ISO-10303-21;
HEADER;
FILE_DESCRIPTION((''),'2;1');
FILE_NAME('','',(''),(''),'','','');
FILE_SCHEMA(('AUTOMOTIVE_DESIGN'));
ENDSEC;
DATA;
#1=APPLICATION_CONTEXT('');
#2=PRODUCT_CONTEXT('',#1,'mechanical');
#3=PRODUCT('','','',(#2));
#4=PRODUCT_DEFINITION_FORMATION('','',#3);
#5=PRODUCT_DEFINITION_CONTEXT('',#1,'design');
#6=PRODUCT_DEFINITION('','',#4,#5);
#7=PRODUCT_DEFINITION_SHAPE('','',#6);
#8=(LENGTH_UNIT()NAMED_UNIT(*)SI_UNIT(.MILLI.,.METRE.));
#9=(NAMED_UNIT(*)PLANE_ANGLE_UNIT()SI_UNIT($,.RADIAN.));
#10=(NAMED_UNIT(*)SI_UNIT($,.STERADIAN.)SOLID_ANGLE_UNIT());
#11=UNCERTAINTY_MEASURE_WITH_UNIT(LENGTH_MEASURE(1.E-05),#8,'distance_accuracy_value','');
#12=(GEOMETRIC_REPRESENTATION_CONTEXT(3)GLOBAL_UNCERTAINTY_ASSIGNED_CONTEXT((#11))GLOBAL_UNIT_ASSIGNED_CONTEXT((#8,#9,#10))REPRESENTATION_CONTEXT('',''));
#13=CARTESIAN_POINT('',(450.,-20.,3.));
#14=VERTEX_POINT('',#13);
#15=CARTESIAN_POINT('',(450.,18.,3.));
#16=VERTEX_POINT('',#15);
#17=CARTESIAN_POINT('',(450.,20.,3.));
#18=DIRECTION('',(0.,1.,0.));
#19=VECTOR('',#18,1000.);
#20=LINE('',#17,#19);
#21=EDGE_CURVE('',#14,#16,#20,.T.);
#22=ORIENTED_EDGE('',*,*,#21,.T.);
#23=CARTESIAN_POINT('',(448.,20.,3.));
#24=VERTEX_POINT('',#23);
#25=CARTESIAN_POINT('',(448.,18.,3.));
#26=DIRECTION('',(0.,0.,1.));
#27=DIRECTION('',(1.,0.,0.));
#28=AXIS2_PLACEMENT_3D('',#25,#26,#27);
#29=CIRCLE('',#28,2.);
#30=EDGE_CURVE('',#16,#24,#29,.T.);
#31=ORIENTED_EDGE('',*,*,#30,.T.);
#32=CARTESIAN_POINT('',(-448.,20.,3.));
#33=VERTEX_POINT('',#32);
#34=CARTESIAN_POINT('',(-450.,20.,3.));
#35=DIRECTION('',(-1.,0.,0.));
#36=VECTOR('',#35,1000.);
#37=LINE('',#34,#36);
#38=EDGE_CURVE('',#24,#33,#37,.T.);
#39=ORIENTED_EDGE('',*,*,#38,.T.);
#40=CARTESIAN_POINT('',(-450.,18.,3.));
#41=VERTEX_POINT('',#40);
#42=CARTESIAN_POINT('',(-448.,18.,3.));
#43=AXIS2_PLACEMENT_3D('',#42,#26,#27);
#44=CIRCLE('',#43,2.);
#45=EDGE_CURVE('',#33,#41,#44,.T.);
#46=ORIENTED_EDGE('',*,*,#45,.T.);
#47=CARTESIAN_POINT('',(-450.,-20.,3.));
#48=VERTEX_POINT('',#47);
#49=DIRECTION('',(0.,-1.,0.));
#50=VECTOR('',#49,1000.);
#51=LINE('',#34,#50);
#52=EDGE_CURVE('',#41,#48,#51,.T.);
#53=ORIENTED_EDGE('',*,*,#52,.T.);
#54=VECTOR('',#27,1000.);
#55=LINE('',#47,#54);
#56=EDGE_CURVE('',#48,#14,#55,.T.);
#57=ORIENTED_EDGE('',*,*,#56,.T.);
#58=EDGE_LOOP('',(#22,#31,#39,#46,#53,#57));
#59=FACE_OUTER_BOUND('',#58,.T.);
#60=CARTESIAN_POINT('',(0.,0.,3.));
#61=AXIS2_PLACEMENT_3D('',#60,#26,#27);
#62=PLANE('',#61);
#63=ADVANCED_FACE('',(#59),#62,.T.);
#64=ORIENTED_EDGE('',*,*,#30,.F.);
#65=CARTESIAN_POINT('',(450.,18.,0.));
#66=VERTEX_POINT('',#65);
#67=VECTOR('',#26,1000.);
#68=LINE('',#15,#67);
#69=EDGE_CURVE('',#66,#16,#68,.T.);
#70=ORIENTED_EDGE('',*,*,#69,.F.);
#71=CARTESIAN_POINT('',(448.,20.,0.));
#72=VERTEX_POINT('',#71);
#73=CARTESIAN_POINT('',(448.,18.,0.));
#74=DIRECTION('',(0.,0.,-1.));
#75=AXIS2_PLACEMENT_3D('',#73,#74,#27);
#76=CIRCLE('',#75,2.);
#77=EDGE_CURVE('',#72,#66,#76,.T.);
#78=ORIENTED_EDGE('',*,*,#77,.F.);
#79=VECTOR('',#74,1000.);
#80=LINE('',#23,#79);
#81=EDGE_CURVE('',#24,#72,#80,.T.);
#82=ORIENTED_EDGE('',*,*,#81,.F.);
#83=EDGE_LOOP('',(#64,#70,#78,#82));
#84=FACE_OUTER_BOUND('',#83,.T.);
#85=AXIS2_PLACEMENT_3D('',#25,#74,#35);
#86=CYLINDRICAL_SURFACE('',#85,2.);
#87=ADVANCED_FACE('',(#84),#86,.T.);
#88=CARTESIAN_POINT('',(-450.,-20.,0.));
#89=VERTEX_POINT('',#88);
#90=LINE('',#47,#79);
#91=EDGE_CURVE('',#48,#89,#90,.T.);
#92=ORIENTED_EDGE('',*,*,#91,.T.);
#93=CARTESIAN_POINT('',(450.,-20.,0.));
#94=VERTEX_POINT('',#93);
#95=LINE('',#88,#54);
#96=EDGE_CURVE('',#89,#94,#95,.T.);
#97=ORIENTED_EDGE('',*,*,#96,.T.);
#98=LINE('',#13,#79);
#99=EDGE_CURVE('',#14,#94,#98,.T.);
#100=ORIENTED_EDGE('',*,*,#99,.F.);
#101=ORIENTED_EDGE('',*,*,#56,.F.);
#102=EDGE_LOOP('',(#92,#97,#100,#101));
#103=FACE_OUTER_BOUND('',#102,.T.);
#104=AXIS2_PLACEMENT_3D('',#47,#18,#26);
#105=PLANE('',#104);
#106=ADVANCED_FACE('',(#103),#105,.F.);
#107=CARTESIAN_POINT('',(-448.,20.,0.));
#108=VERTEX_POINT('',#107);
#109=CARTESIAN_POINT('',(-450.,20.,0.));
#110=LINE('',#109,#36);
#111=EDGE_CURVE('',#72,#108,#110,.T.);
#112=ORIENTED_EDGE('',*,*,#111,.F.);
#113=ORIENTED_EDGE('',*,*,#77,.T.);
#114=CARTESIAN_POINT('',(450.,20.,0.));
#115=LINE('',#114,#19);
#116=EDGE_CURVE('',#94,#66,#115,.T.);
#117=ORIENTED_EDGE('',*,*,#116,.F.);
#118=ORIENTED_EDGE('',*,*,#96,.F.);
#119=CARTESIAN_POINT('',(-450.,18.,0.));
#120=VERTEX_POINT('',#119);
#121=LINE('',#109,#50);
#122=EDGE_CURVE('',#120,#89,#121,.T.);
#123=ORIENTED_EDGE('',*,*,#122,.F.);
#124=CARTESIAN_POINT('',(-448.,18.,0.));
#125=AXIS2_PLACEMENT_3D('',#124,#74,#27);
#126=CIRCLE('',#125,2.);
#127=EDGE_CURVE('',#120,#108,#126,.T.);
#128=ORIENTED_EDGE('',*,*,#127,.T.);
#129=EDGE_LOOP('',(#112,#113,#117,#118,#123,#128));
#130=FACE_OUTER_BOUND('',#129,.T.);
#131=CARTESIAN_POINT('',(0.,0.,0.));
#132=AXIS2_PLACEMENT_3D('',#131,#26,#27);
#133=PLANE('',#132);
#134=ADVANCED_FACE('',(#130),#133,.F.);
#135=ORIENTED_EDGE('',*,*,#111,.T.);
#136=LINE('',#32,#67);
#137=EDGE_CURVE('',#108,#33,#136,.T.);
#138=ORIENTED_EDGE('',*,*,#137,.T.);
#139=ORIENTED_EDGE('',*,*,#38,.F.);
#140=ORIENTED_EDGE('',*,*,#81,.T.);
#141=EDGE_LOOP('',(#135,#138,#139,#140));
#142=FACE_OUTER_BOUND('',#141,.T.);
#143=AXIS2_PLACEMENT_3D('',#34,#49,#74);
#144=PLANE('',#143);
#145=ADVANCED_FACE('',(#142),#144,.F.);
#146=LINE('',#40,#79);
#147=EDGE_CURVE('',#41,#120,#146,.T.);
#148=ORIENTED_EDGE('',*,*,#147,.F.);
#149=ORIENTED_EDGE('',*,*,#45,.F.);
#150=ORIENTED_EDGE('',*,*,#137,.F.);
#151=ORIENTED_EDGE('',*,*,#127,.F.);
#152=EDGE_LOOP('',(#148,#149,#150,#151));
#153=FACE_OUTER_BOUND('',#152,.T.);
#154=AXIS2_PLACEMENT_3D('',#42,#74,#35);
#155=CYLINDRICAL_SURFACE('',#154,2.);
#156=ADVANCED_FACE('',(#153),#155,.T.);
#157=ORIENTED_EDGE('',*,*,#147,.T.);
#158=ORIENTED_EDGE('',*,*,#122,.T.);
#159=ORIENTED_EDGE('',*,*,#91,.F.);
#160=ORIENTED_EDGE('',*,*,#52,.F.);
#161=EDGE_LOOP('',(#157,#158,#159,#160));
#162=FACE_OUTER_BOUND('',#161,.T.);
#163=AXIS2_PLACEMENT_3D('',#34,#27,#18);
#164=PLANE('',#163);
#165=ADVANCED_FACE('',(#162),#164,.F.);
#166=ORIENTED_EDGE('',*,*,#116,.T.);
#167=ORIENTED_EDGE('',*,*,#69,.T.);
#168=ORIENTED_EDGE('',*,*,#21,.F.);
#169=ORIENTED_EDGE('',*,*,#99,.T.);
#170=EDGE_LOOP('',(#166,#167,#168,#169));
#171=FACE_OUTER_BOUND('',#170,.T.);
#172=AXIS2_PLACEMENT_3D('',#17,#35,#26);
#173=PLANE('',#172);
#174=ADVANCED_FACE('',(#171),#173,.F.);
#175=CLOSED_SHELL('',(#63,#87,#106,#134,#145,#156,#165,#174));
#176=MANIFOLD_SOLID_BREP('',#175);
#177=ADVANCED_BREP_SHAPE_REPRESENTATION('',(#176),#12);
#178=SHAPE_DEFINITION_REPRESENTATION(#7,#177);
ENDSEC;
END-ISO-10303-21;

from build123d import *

# Parameters (mm, degrees)
SKETCH_1_W      = 900
SKETCH_1_H      = 40
EXTRUDE_1_DEPTH = 3
FILLET_1_R      = 2


with BuildPart() as part:
    # 草图1 → 凸台-拉伸1 (new body)
    with BuildSketch(Plane.XY):
        Rectangle(SKETCH_1_W, SKETCH_1_H)
    extrude(amount=EXTRUDE_1_DEPTH)

    # 圆角1
    fillet_1_edges = [part.edges().sort_by_distance(p)[0] for p in [
        (-450, 20, 1.5),
        (450, 20, 1.5),
    ]]
    fillet(fillet_1_edges, radius=FILLET_1_R)


solid = part.part
